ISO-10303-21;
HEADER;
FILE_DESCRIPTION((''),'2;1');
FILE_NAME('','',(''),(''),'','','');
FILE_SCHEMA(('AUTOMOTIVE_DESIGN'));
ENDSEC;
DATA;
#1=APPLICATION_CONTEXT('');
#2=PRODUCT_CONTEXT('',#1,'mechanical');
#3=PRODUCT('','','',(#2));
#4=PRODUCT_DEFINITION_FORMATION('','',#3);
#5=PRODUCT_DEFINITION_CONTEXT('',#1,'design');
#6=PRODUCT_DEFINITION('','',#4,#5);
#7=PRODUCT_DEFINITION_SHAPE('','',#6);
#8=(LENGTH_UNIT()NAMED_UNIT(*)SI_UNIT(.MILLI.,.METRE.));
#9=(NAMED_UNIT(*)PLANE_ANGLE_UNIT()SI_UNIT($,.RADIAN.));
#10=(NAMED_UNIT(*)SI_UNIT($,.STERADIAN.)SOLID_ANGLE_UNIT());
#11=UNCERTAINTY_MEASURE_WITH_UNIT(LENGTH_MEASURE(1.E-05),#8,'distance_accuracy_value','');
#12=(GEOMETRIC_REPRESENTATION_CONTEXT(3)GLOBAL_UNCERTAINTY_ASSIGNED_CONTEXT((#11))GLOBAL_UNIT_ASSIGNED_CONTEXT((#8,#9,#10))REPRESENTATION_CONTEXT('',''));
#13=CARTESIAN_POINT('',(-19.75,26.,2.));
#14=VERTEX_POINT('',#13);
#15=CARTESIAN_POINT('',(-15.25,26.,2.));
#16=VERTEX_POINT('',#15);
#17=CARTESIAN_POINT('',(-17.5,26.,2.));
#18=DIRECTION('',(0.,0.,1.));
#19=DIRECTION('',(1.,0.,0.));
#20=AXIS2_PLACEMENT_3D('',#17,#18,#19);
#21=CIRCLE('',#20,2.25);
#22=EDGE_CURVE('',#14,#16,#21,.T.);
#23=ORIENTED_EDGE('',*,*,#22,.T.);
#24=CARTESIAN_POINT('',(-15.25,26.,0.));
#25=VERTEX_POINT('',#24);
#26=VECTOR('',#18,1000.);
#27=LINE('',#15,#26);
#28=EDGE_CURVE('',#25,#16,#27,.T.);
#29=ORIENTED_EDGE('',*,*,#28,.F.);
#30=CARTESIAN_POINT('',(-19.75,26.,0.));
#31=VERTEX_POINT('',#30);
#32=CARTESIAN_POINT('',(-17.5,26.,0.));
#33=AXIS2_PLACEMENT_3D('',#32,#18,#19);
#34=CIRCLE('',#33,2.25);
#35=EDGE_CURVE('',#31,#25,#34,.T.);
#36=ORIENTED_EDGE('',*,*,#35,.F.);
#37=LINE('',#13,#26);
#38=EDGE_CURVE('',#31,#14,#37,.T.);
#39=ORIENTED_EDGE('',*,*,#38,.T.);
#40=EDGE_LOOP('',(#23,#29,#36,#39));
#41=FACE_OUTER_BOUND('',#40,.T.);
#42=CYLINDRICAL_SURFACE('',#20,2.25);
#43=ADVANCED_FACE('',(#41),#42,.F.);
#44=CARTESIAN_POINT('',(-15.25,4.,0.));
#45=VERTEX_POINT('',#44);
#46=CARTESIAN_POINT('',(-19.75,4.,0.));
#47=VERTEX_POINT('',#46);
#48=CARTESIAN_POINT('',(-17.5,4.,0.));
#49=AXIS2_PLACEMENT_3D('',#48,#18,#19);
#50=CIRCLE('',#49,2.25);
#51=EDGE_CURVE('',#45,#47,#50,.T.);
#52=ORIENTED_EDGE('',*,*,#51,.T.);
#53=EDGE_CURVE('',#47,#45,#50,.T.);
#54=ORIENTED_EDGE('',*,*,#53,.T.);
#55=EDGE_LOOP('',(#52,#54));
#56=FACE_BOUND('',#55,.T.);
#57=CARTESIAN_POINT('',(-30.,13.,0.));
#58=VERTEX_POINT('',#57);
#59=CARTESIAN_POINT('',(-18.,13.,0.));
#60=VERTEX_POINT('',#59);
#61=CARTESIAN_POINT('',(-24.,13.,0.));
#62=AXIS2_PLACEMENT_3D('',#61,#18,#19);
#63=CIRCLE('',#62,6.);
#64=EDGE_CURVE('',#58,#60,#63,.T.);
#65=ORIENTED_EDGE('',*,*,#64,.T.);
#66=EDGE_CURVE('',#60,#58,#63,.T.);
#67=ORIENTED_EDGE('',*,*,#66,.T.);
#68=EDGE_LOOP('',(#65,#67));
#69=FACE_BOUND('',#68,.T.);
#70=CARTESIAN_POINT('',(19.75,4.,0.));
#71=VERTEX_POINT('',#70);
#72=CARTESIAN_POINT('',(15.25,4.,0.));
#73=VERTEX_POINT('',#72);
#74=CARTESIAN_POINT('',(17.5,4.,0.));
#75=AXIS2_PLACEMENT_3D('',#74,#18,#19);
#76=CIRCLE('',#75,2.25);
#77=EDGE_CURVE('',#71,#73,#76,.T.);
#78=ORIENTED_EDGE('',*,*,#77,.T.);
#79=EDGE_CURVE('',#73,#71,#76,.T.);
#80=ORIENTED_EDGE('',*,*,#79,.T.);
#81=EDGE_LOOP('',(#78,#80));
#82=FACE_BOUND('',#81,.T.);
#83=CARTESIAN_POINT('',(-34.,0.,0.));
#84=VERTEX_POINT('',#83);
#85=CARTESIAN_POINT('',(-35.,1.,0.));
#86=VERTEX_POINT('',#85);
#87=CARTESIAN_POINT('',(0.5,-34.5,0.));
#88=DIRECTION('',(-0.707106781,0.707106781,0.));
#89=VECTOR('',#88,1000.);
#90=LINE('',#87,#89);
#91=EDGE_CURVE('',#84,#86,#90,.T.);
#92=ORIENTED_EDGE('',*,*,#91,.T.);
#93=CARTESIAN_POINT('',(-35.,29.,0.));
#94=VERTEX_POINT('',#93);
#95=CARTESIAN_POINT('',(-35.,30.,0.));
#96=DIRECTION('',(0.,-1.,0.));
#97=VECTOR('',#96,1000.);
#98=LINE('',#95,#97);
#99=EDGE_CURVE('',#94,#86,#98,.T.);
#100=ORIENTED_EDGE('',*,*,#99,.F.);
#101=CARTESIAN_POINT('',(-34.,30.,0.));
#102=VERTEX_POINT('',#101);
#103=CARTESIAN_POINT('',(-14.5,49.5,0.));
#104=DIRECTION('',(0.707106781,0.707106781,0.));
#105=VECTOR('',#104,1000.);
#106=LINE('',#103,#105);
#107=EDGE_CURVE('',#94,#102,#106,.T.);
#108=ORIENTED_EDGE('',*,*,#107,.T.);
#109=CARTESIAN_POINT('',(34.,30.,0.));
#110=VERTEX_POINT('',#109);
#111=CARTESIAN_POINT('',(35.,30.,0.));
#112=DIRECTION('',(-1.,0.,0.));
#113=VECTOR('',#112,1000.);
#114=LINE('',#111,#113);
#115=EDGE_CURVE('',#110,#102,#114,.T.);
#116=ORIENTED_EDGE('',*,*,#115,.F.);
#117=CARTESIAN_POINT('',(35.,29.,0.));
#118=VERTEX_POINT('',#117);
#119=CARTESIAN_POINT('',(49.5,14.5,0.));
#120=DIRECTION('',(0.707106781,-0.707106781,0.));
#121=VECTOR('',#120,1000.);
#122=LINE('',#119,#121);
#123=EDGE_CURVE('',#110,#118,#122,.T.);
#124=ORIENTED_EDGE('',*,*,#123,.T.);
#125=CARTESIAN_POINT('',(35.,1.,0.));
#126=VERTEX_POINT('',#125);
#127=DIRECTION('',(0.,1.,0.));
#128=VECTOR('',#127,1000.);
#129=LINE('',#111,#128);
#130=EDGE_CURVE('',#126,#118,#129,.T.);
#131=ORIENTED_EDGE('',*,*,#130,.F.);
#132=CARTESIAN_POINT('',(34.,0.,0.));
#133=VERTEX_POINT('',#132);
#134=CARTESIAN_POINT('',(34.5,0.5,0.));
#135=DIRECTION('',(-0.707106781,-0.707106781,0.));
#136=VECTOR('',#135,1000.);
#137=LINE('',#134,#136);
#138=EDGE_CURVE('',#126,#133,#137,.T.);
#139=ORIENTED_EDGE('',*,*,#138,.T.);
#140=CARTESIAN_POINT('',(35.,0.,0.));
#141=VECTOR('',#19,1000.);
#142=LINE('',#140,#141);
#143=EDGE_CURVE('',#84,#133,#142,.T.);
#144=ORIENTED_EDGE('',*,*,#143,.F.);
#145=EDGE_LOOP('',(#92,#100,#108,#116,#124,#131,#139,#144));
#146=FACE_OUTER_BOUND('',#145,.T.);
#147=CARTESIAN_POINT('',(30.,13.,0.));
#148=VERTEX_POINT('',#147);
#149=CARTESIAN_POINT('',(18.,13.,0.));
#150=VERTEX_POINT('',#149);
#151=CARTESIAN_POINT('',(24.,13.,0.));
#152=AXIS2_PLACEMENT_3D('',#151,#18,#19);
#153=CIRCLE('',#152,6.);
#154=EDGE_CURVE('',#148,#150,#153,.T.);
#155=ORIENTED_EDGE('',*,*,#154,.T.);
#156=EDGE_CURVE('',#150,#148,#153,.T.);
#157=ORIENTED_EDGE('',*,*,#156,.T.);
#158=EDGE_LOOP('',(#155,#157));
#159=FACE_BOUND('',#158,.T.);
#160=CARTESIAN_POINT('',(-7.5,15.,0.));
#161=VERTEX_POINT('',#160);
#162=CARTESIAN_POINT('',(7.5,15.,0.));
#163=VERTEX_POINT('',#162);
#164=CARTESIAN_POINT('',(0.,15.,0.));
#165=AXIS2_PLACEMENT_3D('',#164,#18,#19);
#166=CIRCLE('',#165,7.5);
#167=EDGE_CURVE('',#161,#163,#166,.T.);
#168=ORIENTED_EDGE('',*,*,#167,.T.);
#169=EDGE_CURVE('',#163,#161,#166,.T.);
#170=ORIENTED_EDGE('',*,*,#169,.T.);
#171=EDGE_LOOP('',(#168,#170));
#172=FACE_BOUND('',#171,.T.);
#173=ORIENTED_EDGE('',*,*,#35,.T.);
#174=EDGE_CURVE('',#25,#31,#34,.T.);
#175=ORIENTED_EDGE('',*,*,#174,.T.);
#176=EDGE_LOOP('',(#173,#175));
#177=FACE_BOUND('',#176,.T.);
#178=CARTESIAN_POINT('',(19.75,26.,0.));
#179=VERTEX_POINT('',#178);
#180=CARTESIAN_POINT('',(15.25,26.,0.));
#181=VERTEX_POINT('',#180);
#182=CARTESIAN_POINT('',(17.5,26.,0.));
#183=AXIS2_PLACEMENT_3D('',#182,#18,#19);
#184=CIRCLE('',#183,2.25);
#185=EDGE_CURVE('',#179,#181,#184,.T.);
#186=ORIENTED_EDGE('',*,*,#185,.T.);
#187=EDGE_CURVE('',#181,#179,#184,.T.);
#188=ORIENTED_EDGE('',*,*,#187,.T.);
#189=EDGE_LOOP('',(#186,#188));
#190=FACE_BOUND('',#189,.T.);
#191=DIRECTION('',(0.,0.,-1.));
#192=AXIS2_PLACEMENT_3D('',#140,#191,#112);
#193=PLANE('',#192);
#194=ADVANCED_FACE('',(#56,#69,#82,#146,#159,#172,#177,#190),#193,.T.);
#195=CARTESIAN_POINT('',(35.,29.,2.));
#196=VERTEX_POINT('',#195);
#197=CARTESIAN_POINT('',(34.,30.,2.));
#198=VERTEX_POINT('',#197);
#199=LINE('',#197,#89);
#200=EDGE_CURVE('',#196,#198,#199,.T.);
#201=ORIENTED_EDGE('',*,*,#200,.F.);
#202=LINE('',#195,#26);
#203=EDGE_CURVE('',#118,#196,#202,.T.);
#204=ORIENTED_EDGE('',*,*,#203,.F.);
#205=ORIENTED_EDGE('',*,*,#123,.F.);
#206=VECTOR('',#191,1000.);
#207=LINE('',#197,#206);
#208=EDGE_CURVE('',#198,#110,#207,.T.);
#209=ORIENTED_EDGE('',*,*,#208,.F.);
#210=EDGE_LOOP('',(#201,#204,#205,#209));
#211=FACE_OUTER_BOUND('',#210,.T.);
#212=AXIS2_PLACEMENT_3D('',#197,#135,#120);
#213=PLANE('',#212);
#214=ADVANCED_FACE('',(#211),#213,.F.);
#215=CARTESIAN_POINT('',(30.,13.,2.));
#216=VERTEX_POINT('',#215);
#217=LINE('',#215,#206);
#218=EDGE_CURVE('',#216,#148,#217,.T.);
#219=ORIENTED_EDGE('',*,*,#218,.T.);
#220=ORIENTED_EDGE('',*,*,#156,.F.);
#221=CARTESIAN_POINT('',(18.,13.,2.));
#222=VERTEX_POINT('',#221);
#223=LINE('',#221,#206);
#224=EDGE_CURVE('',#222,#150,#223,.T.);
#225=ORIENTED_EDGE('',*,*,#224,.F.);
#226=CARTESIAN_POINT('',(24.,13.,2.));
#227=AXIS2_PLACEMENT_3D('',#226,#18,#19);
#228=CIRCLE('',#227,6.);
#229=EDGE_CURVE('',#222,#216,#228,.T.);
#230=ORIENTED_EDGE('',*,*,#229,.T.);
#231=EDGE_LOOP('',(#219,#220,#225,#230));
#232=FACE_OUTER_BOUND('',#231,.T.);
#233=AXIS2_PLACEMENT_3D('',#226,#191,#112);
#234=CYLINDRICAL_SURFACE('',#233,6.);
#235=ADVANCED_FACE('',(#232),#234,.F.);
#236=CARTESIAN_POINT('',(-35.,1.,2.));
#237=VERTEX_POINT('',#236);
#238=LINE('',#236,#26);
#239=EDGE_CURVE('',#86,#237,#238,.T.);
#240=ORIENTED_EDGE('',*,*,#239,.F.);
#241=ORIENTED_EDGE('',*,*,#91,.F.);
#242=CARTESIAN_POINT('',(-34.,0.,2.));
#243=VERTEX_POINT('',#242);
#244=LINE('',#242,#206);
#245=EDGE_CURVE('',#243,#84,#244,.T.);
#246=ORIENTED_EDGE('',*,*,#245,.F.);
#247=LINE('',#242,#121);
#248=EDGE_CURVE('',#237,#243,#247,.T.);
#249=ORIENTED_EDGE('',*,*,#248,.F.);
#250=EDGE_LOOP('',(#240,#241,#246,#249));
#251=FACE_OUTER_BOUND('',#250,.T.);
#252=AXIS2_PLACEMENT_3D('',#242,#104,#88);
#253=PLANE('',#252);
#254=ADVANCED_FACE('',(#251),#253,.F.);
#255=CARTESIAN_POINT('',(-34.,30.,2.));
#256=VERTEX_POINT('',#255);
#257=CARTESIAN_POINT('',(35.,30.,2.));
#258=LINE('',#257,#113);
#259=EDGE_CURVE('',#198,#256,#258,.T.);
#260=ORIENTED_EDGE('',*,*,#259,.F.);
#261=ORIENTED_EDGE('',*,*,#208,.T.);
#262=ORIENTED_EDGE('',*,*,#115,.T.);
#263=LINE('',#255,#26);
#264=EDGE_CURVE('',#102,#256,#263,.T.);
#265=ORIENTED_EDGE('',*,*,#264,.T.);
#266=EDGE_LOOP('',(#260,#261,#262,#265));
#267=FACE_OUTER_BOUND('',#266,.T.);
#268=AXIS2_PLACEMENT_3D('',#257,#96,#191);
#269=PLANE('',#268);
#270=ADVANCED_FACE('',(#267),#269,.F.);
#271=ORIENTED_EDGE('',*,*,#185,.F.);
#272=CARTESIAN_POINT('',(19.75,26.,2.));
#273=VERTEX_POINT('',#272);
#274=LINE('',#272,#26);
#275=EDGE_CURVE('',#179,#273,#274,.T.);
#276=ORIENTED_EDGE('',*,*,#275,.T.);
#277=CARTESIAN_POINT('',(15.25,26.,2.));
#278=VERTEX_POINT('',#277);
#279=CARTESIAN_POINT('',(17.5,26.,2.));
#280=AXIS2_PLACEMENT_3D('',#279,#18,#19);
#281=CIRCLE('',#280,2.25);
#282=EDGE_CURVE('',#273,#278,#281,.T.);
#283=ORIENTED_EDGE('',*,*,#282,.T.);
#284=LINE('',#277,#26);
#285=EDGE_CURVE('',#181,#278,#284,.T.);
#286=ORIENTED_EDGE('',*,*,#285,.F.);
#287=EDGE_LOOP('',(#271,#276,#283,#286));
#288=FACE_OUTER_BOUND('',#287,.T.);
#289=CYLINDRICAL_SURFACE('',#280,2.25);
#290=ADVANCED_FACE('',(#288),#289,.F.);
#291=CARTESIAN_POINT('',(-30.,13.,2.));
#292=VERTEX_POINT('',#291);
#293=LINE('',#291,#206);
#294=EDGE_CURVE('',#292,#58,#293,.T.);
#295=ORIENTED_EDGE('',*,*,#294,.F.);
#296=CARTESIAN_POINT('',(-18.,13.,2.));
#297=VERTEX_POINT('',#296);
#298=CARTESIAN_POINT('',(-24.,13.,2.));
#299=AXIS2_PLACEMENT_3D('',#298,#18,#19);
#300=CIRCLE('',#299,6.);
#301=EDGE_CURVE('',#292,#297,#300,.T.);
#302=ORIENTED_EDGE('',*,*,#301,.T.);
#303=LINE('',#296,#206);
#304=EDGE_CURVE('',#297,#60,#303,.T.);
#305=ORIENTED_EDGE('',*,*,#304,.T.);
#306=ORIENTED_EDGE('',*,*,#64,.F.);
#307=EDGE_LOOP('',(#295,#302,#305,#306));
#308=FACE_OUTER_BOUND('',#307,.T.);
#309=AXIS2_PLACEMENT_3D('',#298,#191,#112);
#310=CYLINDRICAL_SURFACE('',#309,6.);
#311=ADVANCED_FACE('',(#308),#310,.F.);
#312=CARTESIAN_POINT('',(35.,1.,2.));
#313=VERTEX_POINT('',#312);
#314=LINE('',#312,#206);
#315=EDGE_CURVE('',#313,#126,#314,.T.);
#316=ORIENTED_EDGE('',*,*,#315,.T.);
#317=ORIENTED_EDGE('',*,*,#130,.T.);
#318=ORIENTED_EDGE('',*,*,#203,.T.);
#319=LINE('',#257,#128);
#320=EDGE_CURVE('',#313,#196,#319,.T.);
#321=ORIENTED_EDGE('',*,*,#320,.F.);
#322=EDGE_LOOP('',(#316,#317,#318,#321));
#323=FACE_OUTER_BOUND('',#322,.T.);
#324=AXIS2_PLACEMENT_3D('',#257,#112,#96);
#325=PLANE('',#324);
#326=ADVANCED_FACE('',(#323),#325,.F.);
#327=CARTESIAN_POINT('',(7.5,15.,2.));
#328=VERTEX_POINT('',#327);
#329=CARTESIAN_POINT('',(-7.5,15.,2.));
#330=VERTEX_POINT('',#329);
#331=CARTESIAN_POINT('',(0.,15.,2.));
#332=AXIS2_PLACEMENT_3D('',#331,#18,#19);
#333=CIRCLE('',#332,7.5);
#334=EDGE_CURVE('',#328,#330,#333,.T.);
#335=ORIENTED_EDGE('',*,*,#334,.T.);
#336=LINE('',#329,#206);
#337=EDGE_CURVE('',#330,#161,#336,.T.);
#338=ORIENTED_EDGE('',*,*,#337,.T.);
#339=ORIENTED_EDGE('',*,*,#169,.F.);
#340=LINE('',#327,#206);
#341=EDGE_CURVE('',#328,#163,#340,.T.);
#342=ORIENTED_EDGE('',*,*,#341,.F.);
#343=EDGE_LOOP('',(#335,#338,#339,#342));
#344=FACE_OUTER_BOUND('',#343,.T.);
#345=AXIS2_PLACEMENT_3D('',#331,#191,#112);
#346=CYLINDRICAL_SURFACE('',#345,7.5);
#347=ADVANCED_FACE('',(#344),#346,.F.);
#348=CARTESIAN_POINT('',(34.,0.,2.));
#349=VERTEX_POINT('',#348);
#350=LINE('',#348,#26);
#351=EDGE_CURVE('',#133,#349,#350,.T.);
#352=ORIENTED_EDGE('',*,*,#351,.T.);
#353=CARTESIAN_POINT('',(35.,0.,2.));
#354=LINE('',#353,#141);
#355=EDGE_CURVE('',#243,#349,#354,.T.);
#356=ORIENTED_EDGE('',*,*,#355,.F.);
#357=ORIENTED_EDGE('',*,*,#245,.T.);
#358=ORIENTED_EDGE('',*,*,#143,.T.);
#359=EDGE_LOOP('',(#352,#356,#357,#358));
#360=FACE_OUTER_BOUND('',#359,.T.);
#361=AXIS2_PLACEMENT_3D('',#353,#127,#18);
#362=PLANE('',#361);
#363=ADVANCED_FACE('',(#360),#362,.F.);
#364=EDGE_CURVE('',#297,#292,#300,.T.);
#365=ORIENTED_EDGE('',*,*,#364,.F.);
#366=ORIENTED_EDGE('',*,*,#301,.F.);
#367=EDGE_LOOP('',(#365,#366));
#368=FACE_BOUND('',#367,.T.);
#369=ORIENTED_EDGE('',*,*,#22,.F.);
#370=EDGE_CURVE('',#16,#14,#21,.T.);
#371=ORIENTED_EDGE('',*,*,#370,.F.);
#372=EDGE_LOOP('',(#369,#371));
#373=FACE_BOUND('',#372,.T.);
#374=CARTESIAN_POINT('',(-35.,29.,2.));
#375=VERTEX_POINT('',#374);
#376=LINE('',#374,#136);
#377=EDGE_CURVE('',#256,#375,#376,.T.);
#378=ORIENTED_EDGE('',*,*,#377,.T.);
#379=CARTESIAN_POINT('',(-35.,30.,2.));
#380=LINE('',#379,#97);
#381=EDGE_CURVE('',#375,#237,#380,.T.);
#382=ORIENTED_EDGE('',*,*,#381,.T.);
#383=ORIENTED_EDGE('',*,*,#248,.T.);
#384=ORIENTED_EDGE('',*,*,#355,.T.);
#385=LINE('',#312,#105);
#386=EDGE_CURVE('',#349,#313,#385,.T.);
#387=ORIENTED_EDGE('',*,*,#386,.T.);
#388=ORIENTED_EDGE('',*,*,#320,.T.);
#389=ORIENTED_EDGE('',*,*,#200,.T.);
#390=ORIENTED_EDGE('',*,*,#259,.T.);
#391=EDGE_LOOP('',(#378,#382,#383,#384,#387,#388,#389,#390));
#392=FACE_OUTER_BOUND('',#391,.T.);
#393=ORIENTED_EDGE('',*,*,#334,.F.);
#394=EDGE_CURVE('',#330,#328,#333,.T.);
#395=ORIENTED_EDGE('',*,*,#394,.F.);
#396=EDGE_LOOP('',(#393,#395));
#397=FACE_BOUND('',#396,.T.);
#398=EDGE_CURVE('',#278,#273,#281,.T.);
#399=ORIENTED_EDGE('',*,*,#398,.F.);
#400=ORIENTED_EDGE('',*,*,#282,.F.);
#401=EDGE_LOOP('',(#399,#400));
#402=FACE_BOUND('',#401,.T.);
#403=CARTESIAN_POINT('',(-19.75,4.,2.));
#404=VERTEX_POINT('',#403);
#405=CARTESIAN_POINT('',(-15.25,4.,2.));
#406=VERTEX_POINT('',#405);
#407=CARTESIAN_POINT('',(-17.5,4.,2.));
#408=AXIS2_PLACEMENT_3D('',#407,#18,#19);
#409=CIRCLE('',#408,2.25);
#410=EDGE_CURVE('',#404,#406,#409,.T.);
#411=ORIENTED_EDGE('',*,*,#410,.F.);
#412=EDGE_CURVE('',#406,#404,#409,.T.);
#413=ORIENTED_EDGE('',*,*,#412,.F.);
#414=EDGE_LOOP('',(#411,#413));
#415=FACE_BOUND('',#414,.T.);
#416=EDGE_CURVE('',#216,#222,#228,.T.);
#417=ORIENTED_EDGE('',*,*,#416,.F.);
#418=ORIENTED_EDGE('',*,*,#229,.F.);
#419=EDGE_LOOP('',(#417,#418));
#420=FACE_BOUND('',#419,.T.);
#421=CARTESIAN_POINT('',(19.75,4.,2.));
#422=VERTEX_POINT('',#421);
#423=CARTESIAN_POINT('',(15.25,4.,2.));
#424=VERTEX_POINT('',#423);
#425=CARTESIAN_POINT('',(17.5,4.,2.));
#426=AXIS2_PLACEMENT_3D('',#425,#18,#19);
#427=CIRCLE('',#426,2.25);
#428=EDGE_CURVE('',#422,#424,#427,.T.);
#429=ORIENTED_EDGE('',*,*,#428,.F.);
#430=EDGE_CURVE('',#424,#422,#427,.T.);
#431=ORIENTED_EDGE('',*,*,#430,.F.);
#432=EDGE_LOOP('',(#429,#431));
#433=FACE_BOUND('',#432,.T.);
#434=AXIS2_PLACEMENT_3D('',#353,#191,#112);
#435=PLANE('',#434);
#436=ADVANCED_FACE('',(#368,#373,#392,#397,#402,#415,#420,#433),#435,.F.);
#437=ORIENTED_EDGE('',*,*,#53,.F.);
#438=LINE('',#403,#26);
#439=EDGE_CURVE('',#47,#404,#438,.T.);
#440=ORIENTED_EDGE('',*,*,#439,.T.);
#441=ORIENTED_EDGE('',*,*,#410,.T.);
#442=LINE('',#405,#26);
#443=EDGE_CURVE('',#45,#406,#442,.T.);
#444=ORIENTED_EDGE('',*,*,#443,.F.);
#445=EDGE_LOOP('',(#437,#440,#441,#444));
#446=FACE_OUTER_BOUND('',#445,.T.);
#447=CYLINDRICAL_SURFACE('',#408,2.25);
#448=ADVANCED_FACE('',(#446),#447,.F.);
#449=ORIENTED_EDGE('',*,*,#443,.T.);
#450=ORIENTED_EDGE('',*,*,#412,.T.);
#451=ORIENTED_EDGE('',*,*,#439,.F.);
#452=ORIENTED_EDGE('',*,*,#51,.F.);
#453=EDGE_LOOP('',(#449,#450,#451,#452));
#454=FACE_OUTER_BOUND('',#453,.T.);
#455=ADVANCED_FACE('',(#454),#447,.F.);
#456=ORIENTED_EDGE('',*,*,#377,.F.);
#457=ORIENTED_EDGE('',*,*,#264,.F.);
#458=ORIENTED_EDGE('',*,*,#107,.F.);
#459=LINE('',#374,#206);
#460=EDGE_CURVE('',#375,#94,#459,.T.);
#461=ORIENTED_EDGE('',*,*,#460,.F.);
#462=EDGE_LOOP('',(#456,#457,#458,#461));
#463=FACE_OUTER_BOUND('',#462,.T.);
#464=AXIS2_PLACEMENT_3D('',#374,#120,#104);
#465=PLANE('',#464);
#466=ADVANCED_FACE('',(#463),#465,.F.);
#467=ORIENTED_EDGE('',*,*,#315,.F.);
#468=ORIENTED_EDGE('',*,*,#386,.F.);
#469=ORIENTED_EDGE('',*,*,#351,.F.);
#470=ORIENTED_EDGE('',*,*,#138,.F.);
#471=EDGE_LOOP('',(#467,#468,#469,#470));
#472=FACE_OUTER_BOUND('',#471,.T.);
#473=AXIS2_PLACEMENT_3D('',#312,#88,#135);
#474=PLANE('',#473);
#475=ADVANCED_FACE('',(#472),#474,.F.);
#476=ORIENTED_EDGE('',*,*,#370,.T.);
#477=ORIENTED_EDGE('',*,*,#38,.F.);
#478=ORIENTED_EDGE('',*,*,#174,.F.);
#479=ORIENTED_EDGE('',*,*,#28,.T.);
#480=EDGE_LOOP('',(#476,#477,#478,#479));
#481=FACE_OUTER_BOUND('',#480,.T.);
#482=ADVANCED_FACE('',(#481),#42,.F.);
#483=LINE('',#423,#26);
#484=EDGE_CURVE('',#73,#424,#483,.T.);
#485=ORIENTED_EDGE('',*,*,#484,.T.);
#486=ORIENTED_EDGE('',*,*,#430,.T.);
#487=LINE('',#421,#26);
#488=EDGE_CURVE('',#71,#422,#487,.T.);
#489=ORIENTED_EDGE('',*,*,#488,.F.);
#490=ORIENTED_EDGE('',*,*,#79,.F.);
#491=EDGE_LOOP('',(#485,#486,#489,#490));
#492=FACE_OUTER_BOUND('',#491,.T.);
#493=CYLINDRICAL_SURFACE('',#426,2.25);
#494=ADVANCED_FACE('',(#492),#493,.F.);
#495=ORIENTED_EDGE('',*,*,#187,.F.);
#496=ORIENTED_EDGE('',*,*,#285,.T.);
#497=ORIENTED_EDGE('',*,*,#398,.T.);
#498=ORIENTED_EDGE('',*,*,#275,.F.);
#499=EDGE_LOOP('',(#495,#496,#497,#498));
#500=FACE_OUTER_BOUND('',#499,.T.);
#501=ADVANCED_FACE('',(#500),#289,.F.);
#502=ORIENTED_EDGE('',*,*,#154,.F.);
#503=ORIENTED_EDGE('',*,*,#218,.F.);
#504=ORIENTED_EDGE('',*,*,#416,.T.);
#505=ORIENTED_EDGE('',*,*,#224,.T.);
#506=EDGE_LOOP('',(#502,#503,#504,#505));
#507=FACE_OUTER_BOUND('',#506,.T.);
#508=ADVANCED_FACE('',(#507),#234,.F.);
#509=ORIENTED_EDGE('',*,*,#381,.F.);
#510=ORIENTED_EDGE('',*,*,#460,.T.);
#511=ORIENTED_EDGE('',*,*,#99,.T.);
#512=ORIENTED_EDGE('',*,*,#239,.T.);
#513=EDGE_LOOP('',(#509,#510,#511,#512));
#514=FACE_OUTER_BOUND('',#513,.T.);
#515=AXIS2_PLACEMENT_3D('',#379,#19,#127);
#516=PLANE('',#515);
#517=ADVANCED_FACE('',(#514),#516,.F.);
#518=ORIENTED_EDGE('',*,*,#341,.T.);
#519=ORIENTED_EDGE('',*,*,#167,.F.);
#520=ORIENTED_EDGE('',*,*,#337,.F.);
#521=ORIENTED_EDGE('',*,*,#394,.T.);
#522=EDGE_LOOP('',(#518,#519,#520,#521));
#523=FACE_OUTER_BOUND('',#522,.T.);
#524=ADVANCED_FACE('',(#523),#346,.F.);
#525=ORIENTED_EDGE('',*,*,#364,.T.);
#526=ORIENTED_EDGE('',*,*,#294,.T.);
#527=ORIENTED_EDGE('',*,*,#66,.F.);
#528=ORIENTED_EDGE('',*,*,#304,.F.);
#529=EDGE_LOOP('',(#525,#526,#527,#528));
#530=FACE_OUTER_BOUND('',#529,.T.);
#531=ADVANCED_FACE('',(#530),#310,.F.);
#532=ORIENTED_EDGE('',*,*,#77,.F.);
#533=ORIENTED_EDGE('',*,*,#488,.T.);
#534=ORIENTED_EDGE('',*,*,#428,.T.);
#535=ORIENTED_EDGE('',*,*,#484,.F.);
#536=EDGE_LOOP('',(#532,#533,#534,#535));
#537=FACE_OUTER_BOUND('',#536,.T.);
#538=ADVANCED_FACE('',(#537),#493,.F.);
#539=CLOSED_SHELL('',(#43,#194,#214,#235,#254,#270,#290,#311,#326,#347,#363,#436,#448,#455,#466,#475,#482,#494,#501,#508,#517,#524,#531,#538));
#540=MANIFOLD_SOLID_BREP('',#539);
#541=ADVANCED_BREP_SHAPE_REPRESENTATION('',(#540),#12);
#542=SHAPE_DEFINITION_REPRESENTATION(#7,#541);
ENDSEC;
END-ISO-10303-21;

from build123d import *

# Parameters (mm, degrees)
SKETCH1_W                  = 70
SKETCH1_H                  = 30
SKETCH1_R                  = 6
SKETCH1_R_2                = 7.5
BOSS_EXTRUDE1_DEPTH        = 2
F_4_5_4_5_DIAMETER_HOLE1_D = 4.5
CHAMFER1_SIZE              = 1


with BuildPart() as part:
    # Sketch1 → Boss-Extrude1 (new body)
    with BuildSketch(Plane.XY):
        with Locations((0, 15)):
            Rectangle(SKETCH1_W, SKETCH1_H)
        with Locations((-24, 13)):
            Circle(SKETCH1_R, mode=Mode.SUBTRACT)
        with Locations((24, 13)):
            Circle(SKETCH1_R, mode=Mode.SUBTRACT)
        with Locations((0, 15)):
            Circle(SKETCH1_R_2, mode=Mode.SUBTRACT)
    extrude(amount=BOSS_EXTRUDE1_DEPTH)

    # Ø4.5 (4.5) Diameter Hole1 (through all)
    with Locations(Plane.XY.offset(2)):
        with Locations((-17.5, 26), (17.5, 26), (-17.5, 4), (17.5, 4)):
            Hole(F_4_5_4_5_DIAMETER_HOLE1_D / 2)

    # Chamfer1
    chamfer1_edges = [part.edges().sort_by_distance(p)[0] for p in [
        (35, 0, 1),
        (-35, 0, 1),
        (-35, 30, 1),
        (35, 30, 1),
    ]]
    chamfer(chamfer1_edges, length=CHAMFER1_SIZE)


solid = part.part
